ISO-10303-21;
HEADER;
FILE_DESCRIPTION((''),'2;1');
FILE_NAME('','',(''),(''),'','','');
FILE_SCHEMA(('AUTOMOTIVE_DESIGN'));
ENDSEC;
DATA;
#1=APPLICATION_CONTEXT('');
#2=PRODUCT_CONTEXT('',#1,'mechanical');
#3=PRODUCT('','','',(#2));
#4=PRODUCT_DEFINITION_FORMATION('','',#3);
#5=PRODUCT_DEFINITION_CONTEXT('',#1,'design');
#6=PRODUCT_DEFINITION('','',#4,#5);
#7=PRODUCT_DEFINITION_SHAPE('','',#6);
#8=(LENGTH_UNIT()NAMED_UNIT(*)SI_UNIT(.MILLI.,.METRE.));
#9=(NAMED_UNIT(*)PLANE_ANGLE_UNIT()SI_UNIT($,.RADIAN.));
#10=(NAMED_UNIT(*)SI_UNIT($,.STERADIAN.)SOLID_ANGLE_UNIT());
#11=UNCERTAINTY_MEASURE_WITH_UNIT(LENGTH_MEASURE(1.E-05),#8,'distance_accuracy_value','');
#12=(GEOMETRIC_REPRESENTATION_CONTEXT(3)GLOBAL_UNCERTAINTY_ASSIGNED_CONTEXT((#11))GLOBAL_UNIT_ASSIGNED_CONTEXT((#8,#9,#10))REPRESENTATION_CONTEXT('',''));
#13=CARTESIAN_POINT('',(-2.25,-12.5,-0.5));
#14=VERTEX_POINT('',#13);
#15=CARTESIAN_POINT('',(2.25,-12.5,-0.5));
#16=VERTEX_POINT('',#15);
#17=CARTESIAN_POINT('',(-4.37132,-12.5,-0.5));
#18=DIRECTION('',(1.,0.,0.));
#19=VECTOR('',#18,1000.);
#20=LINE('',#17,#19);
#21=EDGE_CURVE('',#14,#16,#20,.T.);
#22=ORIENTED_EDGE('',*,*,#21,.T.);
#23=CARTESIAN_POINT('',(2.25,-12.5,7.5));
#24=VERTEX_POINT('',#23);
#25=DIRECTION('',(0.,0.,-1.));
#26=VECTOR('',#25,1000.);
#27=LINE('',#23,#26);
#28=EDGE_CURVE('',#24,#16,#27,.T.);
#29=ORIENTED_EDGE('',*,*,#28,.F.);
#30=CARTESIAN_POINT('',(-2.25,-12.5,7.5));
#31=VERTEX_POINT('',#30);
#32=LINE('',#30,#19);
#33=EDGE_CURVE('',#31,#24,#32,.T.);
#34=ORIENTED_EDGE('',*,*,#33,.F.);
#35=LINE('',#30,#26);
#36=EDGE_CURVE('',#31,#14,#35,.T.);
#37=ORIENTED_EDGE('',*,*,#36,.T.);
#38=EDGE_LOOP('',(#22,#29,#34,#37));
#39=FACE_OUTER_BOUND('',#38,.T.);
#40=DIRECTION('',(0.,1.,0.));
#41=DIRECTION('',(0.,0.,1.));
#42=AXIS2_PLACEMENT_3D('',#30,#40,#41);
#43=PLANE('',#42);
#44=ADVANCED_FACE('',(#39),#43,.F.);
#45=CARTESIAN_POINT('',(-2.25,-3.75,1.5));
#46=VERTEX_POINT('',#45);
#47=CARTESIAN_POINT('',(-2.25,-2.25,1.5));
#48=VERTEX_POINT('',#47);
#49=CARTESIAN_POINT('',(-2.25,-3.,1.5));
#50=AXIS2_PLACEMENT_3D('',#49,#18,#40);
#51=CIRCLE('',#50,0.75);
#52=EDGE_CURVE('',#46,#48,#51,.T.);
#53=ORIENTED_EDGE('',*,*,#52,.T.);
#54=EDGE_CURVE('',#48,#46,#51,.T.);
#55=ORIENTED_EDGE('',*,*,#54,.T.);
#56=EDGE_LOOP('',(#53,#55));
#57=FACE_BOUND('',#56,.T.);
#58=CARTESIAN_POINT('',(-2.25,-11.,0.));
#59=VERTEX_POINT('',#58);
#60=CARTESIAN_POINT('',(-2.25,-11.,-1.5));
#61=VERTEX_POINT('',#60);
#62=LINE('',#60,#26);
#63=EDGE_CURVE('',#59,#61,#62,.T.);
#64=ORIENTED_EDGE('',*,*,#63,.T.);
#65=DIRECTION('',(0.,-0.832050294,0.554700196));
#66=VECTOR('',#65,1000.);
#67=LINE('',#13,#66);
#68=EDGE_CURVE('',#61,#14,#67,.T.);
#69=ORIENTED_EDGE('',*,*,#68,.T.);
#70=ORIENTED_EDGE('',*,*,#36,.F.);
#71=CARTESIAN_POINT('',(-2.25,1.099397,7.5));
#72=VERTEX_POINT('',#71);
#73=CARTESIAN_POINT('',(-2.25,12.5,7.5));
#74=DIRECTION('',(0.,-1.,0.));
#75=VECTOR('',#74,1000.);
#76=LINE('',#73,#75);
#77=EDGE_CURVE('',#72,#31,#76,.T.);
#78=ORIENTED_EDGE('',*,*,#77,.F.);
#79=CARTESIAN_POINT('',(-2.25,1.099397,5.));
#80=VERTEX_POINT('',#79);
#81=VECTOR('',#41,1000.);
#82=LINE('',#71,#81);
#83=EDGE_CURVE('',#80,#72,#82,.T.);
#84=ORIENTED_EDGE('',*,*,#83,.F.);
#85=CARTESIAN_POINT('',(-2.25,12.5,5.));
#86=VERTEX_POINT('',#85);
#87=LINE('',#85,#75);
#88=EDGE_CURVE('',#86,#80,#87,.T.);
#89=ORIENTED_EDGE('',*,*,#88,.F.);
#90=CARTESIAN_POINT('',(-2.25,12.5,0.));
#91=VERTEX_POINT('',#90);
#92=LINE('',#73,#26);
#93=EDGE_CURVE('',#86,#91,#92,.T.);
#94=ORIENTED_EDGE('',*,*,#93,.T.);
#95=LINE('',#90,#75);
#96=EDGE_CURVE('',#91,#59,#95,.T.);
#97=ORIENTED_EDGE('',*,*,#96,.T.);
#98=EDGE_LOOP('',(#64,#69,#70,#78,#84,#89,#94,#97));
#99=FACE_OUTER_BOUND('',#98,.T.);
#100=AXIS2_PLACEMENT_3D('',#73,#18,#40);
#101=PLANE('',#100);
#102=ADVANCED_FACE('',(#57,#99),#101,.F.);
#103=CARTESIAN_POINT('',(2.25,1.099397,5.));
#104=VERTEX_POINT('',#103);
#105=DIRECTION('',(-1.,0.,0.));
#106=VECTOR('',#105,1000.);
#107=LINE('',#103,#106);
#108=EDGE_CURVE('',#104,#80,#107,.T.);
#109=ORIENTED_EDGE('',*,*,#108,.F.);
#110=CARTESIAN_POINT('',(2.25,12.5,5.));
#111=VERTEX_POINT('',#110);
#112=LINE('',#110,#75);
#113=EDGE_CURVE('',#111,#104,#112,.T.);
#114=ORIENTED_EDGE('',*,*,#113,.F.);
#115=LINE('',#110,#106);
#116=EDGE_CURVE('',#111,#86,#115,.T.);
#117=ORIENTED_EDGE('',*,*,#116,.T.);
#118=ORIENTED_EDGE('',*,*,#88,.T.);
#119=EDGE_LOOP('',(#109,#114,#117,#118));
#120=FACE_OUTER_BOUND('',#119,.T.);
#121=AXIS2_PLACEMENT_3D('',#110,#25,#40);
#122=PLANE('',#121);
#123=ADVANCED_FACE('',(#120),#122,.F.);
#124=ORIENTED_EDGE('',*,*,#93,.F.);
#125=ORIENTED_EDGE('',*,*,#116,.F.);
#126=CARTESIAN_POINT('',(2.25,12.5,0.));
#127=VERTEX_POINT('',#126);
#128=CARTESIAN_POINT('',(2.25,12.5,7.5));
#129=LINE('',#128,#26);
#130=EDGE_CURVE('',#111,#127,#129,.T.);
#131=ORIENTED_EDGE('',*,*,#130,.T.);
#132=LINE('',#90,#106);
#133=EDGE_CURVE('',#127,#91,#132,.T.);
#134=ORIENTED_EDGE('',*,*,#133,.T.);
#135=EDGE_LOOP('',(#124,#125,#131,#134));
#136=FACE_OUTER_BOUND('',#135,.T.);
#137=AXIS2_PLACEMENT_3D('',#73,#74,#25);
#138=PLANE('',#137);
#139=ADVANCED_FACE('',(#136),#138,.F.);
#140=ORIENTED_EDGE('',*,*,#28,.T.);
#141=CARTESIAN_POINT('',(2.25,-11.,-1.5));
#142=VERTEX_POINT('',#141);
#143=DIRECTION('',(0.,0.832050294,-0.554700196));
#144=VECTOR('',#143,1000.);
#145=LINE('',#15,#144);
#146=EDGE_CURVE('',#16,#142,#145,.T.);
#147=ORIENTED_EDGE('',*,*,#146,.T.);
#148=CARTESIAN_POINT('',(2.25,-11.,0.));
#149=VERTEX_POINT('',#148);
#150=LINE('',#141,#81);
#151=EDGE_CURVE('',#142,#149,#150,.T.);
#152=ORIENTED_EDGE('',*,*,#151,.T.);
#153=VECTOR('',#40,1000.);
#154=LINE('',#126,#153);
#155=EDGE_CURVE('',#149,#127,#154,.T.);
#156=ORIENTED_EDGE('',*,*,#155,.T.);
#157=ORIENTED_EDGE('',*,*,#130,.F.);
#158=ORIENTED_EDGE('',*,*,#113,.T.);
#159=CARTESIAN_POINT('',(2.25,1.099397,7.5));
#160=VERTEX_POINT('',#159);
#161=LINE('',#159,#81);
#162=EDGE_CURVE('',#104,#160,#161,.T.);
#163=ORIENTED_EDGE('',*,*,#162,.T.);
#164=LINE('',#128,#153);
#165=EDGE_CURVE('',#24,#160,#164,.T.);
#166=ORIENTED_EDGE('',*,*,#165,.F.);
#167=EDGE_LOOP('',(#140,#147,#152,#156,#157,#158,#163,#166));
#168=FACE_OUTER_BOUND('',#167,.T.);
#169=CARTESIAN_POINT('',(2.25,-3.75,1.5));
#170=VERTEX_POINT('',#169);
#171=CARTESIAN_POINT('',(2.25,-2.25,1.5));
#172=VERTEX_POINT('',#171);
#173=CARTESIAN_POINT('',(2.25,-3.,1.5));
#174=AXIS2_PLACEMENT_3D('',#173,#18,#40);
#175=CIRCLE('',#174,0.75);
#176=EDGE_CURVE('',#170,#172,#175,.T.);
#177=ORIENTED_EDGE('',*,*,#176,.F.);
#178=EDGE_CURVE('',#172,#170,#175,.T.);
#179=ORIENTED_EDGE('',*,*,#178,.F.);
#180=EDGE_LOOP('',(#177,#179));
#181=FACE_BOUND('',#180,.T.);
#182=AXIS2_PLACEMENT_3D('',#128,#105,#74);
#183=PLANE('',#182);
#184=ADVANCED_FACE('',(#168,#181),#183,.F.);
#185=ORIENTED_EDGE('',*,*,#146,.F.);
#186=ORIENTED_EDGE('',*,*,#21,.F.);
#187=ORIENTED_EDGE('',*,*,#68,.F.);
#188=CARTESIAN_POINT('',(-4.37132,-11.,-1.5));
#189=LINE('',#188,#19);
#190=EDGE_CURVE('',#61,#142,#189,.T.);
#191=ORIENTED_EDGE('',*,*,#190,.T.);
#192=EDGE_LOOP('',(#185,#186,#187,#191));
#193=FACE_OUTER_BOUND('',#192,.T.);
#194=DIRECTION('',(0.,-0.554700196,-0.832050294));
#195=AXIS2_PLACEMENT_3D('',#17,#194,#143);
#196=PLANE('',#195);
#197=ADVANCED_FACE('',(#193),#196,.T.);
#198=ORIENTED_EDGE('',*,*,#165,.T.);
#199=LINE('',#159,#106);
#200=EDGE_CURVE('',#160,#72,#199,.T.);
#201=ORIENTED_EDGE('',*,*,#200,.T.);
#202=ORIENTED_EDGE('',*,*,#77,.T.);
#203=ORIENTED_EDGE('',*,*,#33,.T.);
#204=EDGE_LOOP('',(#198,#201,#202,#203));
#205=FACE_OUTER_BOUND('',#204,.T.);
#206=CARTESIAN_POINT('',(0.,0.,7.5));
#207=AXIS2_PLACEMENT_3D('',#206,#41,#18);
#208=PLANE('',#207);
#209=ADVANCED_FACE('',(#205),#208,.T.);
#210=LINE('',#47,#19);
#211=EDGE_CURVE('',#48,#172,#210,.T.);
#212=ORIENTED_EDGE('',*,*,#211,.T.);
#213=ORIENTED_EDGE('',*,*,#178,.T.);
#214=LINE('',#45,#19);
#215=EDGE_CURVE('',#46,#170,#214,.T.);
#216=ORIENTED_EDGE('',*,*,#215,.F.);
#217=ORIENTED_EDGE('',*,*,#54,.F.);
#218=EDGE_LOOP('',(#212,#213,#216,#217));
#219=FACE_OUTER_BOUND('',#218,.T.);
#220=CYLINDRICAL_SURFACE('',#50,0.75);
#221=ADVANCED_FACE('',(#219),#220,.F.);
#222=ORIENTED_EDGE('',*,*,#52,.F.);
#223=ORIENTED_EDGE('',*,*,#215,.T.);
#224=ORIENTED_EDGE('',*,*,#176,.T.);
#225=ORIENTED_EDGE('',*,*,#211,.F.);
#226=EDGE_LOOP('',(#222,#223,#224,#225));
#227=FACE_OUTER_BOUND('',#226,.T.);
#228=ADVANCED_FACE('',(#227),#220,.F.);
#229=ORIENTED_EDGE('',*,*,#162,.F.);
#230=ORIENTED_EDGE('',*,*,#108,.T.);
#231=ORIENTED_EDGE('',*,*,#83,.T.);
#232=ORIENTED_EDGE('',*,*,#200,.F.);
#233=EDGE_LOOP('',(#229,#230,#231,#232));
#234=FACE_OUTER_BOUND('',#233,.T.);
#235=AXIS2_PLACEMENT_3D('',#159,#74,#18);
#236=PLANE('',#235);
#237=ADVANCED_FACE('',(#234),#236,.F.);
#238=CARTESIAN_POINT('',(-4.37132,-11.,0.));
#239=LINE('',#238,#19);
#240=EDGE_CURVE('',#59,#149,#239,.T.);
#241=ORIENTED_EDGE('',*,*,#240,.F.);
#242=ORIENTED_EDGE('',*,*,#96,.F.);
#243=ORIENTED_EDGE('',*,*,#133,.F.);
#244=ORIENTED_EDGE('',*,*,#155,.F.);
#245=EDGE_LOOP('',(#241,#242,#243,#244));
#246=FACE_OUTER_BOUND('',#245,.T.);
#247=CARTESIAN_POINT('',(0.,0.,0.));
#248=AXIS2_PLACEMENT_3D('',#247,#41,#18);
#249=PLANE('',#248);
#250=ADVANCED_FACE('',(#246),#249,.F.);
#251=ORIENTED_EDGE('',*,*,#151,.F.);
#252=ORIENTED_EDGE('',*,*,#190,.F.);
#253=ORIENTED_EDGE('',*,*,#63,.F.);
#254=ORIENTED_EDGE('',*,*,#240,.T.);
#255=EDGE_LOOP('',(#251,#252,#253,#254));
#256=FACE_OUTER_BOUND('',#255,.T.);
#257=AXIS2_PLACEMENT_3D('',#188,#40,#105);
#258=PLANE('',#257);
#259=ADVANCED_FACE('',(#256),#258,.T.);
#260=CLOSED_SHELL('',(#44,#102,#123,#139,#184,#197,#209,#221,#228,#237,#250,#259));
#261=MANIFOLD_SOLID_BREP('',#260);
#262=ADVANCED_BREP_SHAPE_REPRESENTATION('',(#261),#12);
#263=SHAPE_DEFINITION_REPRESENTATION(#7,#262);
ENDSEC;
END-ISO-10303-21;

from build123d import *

# Parameters (mm, degrees)
SKETCH43_W          = 4.5
SKETCH43_H          = 25
BOSS_EXTRUDE1_DEPTH = 7.5
BOSS_EXTRUDE2_DEPTH = 4.5
SKETCH45_R          = 0.75
CUT_EXTRUDE1_DEPTH  = 16.256146302
SKETCH46_W          = 2.5
SKETCH46_H          = 11.400602873
CUT_EXTRUDE2_DEPTH  = 16.256146302


with BuildPart() as part:
    # Sketch43 → Boss-Extrude1 (new body)
    with BuildSketch(Plane.XY):
        Rectangle(SKETCH43_W, SKETCH43_H)
    extrude(amount=BOSS_EXTRUDE1_DEPTH)

    # Sketch44 → Boss-Extrude2 (add)
    with BuildSketch(Plane(origin=(2.25, 0, 0), x_dir=(0, 0, -1), z_dir=(1, 0, 0))):
        Polygon((0, -12.5), (0.5, -12.5), (1.5, -11), (0, -11), align=None)
    extrude(amount=-BOSS_EXTRUDE2_DEPTH)

    # Sketch45 → Cut-Extrude1 (cut, through all)
    with BuildSketch(Plane(origin=(2.25, 0, 0), x_dir=(0, 0, -1), z_dir=(1, 0, 0))):
        with Locations(Location((-1.5, -3, 0), (0, 0, 90))):
            Circle(SKETCH45_R)
    extrude(amount=-CUT_EXTRUDE1_DEPTH, mode=Mode.SUBTRACT)

    # Sketch46 → Cut-Extrude2 (cut, through all)
    with BuildSketch(Plane.ZY.offset(2.25)):
        with Locations((6.25, 6.799698563)):
            Rectangle(SKETCH46_W, SKETCH46_H)
    extrude(amount=-CUT_EXTRUDE2_DEPTH, mode=Mode.SUBTRACT)


solid = part.part
